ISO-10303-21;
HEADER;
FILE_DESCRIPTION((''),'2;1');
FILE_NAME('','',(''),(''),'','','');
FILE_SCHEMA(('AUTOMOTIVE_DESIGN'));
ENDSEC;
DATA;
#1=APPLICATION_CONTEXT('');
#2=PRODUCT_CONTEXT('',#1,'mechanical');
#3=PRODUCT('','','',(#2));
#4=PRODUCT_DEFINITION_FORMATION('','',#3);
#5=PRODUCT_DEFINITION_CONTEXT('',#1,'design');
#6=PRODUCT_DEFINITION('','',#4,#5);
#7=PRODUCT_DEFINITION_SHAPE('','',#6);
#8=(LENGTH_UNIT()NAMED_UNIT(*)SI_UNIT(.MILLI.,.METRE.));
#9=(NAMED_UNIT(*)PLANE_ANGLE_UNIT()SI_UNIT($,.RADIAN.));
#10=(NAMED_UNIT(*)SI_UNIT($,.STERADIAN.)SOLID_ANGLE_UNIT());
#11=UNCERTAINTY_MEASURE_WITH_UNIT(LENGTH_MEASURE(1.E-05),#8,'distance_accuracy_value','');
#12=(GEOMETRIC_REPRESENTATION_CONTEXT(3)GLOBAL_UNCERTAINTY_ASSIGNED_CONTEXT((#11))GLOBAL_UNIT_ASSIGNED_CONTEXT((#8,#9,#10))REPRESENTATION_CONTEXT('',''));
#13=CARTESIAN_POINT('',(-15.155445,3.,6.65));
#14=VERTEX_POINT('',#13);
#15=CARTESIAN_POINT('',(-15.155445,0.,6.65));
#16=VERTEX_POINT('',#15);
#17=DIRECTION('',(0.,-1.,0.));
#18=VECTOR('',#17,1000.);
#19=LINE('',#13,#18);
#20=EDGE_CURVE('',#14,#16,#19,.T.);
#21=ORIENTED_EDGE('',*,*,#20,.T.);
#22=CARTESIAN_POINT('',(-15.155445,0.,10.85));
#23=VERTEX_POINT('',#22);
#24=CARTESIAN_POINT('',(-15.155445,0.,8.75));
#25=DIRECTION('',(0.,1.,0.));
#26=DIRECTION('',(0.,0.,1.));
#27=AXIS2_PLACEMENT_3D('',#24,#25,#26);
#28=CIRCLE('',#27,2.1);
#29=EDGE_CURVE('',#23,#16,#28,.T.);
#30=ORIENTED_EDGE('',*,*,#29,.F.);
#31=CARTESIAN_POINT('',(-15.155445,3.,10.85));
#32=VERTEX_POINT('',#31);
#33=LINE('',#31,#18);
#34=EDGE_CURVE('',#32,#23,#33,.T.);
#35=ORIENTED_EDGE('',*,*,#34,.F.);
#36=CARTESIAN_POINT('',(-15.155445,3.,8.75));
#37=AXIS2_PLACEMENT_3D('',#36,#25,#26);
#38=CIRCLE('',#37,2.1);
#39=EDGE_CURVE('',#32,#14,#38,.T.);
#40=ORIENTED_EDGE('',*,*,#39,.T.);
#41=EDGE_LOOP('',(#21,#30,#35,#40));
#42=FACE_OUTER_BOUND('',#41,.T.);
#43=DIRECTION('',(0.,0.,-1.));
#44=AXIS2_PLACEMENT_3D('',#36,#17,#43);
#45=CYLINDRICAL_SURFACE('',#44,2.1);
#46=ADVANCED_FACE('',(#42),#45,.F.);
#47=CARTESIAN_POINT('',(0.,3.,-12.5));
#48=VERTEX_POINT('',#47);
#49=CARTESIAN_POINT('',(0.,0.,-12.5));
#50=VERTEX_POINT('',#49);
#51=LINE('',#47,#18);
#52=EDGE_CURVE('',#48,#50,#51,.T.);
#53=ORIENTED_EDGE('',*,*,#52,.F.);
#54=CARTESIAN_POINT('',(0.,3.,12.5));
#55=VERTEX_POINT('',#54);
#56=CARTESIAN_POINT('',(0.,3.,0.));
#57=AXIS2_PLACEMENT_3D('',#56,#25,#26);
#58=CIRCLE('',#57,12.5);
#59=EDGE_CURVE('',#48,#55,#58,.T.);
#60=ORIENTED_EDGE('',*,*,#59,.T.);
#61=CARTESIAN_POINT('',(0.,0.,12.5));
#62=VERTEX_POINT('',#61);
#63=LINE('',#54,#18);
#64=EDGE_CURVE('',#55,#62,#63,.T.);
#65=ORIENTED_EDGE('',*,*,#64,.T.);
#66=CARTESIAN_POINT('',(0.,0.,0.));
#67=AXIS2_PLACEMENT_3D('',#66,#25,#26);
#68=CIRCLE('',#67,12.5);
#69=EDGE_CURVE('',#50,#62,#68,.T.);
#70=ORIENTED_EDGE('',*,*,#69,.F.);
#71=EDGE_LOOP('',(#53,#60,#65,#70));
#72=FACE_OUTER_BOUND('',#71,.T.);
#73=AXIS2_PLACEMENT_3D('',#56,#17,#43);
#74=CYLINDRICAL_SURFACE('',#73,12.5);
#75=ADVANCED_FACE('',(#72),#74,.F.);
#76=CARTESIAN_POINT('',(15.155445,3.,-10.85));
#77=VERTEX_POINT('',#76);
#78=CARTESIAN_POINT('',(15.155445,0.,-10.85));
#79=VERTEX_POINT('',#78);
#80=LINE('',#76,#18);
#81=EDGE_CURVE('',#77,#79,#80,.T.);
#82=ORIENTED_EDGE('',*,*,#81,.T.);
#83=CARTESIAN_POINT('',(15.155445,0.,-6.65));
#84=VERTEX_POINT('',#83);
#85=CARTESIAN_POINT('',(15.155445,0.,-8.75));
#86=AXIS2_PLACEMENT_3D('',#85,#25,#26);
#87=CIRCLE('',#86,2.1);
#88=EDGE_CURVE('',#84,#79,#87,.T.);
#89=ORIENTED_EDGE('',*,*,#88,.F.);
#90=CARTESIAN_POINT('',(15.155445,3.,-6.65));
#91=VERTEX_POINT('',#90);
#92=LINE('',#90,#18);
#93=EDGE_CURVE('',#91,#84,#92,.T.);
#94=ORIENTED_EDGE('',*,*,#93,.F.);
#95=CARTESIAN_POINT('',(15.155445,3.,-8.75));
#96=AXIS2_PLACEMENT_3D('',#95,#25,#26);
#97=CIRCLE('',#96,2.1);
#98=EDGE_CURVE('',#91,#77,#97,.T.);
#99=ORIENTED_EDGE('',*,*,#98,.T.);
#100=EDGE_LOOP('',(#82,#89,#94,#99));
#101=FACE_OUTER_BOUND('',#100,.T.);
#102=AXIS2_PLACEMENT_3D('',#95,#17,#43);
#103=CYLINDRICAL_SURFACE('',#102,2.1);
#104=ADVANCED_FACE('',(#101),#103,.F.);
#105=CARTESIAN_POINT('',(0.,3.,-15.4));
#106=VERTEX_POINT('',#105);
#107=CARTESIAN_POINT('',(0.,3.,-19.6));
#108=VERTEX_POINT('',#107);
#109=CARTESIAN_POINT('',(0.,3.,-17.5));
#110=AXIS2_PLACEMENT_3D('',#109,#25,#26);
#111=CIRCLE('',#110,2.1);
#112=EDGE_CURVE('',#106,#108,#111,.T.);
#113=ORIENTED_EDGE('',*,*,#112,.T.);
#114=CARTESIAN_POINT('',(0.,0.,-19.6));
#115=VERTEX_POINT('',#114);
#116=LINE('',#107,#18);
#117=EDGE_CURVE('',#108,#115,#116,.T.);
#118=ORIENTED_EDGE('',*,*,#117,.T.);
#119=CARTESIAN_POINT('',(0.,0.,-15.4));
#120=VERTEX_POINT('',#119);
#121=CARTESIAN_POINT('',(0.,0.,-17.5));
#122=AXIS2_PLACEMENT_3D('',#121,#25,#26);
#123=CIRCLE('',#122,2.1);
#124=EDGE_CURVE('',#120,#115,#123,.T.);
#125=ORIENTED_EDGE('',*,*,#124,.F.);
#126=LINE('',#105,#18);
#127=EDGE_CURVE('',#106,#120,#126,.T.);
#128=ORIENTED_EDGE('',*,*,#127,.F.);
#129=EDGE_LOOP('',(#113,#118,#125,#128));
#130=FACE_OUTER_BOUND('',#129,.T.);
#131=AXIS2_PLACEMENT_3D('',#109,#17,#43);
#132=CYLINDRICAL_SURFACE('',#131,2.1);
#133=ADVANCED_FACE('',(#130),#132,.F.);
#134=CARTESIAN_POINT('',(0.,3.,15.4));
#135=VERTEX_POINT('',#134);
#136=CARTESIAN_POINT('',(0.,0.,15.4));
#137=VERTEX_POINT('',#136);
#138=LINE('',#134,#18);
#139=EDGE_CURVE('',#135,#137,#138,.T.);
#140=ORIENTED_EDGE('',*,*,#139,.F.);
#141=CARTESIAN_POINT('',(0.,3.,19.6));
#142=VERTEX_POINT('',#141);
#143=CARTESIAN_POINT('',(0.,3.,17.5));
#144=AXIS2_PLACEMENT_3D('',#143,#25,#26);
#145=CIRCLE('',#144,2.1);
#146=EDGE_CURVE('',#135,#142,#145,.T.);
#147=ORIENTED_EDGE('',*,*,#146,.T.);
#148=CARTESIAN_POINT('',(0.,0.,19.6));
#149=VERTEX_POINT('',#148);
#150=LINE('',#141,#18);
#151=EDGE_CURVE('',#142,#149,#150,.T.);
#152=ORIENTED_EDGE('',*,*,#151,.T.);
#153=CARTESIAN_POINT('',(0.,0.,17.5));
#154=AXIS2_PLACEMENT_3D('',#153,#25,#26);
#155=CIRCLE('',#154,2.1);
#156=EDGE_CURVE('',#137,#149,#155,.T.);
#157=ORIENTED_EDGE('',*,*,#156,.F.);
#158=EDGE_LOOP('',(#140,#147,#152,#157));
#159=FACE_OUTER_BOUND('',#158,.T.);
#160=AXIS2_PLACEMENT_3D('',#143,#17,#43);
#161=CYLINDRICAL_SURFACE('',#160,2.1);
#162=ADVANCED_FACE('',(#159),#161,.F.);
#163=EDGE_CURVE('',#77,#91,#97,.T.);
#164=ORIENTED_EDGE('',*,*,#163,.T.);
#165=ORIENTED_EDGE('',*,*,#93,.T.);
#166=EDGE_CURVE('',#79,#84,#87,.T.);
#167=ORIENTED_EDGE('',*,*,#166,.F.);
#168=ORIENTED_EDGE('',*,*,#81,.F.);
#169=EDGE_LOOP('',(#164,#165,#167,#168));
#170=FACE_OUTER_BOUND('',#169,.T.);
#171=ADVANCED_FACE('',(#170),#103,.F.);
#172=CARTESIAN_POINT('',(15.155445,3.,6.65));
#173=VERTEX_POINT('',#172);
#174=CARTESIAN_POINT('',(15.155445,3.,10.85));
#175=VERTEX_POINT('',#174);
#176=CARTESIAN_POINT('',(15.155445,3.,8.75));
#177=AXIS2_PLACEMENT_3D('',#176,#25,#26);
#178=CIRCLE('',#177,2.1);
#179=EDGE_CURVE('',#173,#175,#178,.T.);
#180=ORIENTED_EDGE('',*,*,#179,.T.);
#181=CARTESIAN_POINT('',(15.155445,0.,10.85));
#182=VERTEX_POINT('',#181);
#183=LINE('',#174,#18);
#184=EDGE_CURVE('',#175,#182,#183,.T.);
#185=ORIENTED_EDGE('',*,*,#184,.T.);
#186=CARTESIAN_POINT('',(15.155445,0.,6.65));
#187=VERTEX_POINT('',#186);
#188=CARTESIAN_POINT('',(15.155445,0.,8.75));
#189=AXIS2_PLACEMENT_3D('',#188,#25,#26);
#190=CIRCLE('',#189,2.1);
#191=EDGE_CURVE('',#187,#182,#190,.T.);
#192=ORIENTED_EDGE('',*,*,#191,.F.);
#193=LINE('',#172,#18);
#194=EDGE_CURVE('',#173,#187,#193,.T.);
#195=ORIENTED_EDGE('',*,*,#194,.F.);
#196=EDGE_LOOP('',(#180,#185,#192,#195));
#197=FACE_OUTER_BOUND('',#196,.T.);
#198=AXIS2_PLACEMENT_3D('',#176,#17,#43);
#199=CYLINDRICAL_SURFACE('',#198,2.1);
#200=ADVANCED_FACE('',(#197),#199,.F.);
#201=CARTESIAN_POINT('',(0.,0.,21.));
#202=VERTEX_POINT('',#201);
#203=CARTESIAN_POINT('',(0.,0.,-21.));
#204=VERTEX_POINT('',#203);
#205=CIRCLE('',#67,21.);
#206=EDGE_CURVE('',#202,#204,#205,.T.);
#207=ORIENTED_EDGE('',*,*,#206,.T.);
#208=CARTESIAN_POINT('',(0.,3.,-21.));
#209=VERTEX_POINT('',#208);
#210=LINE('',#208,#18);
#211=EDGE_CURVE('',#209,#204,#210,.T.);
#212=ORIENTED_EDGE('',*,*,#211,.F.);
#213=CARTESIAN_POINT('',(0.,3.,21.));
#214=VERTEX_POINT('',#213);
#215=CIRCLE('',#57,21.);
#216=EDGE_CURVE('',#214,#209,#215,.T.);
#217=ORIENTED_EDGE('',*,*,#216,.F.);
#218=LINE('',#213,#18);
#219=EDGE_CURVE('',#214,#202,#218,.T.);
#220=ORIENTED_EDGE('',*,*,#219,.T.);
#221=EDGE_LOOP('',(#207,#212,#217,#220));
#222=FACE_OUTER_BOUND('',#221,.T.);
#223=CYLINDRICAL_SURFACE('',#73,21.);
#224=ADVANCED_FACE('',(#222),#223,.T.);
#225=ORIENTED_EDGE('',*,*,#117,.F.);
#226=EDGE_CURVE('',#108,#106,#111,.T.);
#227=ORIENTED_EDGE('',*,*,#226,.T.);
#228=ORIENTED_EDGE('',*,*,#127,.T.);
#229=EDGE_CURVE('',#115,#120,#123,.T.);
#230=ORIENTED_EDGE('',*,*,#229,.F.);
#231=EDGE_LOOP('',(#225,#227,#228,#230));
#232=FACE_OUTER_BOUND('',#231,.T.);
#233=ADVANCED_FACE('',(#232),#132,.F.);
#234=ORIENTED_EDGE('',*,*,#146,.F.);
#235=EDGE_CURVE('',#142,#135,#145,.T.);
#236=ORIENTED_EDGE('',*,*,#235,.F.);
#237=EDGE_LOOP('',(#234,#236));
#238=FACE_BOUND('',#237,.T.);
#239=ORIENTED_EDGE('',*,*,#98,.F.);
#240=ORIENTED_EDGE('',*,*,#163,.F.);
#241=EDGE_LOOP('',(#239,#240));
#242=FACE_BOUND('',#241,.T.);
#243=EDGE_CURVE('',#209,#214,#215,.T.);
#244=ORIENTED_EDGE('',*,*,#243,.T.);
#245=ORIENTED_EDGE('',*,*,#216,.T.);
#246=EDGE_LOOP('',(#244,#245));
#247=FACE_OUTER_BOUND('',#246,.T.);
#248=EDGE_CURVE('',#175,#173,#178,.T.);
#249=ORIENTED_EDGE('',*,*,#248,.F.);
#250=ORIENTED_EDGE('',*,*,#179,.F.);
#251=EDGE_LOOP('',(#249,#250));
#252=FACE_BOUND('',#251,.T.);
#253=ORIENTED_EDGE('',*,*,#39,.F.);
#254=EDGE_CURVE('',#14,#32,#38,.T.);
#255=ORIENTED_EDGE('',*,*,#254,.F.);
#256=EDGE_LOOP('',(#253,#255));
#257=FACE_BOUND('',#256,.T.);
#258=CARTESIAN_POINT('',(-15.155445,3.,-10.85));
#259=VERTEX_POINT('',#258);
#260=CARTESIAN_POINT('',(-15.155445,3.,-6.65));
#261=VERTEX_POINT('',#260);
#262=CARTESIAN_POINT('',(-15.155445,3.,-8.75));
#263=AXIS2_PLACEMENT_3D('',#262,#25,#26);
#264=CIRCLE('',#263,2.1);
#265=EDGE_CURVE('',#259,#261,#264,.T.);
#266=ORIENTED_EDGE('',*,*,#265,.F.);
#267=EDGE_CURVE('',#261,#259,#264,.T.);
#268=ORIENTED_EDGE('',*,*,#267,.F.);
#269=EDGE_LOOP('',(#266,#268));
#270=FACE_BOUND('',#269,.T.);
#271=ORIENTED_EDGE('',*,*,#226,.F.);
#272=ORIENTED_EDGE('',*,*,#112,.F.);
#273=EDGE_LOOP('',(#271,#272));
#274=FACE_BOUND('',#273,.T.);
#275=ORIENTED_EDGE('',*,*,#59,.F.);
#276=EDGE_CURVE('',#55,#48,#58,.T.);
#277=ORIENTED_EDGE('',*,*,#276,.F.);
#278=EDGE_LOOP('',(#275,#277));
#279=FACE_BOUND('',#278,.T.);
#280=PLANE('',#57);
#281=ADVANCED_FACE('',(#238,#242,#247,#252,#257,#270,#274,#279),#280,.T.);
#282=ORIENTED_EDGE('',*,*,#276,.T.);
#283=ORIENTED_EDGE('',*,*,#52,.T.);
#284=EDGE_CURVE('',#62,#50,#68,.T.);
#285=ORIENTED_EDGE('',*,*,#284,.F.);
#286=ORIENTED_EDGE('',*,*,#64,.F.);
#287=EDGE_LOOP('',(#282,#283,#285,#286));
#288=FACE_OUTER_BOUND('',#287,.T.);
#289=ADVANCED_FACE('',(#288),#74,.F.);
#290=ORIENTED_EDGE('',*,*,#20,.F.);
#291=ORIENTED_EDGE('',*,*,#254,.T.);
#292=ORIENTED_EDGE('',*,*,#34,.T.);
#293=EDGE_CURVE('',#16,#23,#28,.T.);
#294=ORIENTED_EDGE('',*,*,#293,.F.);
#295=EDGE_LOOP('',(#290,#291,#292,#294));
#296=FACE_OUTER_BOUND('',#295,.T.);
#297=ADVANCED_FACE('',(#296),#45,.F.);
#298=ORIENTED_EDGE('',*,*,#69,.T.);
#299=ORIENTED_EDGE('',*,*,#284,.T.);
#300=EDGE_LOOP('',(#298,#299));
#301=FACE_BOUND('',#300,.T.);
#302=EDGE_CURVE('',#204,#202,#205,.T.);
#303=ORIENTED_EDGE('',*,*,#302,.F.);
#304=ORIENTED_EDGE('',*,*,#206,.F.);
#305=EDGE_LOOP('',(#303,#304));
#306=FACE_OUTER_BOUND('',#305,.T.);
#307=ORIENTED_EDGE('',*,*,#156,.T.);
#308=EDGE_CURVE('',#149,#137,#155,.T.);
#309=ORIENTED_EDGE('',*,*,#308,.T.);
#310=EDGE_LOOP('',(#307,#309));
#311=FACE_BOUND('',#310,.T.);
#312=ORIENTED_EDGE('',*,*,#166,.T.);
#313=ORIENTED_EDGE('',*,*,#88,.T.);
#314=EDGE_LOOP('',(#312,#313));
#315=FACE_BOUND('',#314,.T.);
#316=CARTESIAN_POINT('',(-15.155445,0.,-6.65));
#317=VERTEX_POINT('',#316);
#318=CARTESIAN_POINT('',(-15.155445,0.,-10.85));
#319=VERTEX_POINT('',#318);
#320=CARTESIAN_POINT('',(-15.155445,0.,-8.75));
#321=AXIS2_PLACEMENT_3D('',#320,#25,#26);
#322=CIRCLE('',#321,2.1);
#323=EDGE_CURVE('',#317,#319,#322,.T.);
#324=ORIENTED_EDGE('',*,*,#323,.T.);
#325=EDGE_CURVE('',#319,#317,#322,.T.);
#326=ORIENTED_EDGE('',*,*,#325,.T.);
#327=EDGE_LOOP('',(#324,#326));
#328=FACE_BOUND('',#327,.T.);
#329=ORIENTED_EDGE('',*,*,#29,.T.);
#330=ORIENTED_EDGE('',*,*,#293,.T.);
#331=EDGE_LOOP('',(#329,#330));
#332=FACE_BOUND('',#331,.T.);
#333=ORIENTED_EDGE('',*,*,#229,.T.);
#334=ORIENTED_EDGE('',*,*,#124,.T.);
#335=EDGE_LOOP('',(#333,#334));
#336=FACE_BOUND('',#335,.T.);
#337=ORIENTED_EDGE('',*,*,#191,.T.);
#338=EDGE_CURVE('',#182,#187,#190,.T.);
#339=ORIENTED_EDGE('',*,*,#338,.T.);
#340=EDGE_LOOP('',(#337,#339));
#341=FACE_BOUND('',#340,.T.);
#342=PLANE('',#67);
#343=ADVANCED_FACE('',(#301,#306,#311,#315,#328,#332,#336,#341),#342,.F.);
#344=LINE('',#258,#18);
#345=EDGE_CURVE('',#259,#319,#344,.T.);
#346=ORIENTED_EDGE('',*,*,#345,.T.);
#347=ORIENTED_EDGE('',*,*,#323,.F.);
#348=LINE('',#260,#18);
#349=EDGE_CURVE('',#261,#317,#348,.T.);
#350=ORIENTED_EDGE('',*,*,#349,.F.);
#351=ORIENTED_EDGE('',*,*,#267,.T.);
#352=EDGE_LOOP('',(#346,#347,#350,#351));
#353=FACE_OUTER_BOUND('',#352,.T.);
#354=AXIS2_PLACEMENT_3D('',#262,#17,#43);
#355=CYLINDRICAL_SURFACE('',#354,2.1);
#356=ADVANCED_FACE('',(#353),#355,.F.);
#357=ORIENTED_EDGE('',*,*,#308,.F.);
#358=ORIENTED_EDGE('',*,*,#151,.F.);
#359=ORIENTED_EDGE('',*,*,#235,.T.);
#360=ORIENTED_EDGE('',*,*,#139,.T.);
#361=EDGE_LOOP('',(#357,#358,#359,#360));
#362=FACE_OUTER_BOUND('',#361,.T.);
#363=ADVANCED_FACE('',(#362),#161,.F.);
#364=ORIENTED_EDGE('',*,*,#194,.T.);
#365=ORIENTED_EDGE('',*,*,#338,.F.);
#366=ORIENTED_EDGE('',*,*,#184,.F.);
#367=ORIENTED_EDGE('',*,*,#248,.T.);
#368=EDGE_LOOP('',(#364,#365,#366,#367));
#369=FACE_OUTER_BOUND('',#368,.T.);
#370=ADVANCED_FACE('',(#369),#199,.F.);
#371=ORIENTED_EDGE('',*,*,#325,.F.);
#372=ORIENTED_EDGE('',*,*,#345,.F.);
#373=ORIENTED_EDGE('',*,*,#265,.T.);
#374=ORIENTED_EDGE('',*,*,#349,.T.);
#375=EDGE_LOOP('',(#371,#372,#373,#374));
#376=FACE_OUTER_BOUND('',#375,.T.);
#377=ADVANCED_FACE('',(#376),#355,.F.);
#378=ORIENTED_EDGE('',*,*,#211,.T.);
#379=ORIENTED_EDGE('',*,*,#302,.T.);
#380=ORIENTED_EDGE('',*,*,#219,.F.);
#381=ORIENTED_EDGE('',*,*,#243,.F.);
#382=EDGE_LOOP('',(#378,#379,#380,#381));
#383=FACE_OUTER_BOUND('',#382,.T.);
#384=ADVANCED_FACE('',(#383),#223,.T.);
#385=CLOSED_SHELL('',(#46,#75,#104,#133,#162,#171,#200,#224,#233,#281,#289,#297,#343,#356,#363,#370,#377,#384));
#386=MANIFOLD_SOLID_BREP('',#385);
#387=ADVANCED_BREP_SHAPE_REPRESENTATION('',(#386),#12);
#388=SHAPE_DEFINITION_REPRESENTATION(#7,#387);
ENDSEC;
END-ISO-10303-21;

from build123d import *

# Parameters (mm, degrees)
SKETCH_1_R      = 21
SKETCH_1_R_2    = 12.5
SKETCH_1_R_3    = 2.1
EXTRUDE_1_DEPTH = 3


with BuildPart() as part:
    # 草图1 → 凸台-拉伸1 (new body)
    with BuildSketch(Plane(origin=(0, 0, 0), x_dir=(1, 0, 0), z_dir=(0, 1, 0))):
        with Locations(Location((0, 0, 0), (0, 0, 270))):
            Circle(SKETCH_1_R)
        with Locations(Location((0, 0, 0), (0, 0, 270))):
            Circle(SKETCH_1_R_2, mode=Mode.SUBTRACT)
        with Locations(Location((0, 17.5, 0), (0, 0, 270))):
            Circle(SKETCH_1_R_3, mode=Mode.SUBTRACT)
        with Locations(Location((15.155444566, 8.75, 0), (0, 0, 270))):
            Circle(SKETCH_1_R_3, mode=Mode.SUBTRACT)
        with Locations(Location((15.155444566, -8.75, 0), (0, 0, 270))):
            Circle(SKETCH_1_R_3, mode=Mode.SUBTRACT)
        with Locations(Location((0, -17.5, 0), (0, 0, 270))):
            Circle(SKETCH_1_R_3, mode=Mode.SUBTRACT)
        with Locations(Location((-15.155444566, -8.75, 0), (0, 0, 270))):
            Circle(SKETCH_1_R_3, mode=Mode.SUBTRACT)
        with Locations(Location((-15.155444566, 8.75, 0), (0, 0, 270))):
            Circle(SKETCH_1_R_3, mode=Mode.SUBTRACT)
    extrude(amount=EXTRUDE_1_DEPTH)


solid = part.part
